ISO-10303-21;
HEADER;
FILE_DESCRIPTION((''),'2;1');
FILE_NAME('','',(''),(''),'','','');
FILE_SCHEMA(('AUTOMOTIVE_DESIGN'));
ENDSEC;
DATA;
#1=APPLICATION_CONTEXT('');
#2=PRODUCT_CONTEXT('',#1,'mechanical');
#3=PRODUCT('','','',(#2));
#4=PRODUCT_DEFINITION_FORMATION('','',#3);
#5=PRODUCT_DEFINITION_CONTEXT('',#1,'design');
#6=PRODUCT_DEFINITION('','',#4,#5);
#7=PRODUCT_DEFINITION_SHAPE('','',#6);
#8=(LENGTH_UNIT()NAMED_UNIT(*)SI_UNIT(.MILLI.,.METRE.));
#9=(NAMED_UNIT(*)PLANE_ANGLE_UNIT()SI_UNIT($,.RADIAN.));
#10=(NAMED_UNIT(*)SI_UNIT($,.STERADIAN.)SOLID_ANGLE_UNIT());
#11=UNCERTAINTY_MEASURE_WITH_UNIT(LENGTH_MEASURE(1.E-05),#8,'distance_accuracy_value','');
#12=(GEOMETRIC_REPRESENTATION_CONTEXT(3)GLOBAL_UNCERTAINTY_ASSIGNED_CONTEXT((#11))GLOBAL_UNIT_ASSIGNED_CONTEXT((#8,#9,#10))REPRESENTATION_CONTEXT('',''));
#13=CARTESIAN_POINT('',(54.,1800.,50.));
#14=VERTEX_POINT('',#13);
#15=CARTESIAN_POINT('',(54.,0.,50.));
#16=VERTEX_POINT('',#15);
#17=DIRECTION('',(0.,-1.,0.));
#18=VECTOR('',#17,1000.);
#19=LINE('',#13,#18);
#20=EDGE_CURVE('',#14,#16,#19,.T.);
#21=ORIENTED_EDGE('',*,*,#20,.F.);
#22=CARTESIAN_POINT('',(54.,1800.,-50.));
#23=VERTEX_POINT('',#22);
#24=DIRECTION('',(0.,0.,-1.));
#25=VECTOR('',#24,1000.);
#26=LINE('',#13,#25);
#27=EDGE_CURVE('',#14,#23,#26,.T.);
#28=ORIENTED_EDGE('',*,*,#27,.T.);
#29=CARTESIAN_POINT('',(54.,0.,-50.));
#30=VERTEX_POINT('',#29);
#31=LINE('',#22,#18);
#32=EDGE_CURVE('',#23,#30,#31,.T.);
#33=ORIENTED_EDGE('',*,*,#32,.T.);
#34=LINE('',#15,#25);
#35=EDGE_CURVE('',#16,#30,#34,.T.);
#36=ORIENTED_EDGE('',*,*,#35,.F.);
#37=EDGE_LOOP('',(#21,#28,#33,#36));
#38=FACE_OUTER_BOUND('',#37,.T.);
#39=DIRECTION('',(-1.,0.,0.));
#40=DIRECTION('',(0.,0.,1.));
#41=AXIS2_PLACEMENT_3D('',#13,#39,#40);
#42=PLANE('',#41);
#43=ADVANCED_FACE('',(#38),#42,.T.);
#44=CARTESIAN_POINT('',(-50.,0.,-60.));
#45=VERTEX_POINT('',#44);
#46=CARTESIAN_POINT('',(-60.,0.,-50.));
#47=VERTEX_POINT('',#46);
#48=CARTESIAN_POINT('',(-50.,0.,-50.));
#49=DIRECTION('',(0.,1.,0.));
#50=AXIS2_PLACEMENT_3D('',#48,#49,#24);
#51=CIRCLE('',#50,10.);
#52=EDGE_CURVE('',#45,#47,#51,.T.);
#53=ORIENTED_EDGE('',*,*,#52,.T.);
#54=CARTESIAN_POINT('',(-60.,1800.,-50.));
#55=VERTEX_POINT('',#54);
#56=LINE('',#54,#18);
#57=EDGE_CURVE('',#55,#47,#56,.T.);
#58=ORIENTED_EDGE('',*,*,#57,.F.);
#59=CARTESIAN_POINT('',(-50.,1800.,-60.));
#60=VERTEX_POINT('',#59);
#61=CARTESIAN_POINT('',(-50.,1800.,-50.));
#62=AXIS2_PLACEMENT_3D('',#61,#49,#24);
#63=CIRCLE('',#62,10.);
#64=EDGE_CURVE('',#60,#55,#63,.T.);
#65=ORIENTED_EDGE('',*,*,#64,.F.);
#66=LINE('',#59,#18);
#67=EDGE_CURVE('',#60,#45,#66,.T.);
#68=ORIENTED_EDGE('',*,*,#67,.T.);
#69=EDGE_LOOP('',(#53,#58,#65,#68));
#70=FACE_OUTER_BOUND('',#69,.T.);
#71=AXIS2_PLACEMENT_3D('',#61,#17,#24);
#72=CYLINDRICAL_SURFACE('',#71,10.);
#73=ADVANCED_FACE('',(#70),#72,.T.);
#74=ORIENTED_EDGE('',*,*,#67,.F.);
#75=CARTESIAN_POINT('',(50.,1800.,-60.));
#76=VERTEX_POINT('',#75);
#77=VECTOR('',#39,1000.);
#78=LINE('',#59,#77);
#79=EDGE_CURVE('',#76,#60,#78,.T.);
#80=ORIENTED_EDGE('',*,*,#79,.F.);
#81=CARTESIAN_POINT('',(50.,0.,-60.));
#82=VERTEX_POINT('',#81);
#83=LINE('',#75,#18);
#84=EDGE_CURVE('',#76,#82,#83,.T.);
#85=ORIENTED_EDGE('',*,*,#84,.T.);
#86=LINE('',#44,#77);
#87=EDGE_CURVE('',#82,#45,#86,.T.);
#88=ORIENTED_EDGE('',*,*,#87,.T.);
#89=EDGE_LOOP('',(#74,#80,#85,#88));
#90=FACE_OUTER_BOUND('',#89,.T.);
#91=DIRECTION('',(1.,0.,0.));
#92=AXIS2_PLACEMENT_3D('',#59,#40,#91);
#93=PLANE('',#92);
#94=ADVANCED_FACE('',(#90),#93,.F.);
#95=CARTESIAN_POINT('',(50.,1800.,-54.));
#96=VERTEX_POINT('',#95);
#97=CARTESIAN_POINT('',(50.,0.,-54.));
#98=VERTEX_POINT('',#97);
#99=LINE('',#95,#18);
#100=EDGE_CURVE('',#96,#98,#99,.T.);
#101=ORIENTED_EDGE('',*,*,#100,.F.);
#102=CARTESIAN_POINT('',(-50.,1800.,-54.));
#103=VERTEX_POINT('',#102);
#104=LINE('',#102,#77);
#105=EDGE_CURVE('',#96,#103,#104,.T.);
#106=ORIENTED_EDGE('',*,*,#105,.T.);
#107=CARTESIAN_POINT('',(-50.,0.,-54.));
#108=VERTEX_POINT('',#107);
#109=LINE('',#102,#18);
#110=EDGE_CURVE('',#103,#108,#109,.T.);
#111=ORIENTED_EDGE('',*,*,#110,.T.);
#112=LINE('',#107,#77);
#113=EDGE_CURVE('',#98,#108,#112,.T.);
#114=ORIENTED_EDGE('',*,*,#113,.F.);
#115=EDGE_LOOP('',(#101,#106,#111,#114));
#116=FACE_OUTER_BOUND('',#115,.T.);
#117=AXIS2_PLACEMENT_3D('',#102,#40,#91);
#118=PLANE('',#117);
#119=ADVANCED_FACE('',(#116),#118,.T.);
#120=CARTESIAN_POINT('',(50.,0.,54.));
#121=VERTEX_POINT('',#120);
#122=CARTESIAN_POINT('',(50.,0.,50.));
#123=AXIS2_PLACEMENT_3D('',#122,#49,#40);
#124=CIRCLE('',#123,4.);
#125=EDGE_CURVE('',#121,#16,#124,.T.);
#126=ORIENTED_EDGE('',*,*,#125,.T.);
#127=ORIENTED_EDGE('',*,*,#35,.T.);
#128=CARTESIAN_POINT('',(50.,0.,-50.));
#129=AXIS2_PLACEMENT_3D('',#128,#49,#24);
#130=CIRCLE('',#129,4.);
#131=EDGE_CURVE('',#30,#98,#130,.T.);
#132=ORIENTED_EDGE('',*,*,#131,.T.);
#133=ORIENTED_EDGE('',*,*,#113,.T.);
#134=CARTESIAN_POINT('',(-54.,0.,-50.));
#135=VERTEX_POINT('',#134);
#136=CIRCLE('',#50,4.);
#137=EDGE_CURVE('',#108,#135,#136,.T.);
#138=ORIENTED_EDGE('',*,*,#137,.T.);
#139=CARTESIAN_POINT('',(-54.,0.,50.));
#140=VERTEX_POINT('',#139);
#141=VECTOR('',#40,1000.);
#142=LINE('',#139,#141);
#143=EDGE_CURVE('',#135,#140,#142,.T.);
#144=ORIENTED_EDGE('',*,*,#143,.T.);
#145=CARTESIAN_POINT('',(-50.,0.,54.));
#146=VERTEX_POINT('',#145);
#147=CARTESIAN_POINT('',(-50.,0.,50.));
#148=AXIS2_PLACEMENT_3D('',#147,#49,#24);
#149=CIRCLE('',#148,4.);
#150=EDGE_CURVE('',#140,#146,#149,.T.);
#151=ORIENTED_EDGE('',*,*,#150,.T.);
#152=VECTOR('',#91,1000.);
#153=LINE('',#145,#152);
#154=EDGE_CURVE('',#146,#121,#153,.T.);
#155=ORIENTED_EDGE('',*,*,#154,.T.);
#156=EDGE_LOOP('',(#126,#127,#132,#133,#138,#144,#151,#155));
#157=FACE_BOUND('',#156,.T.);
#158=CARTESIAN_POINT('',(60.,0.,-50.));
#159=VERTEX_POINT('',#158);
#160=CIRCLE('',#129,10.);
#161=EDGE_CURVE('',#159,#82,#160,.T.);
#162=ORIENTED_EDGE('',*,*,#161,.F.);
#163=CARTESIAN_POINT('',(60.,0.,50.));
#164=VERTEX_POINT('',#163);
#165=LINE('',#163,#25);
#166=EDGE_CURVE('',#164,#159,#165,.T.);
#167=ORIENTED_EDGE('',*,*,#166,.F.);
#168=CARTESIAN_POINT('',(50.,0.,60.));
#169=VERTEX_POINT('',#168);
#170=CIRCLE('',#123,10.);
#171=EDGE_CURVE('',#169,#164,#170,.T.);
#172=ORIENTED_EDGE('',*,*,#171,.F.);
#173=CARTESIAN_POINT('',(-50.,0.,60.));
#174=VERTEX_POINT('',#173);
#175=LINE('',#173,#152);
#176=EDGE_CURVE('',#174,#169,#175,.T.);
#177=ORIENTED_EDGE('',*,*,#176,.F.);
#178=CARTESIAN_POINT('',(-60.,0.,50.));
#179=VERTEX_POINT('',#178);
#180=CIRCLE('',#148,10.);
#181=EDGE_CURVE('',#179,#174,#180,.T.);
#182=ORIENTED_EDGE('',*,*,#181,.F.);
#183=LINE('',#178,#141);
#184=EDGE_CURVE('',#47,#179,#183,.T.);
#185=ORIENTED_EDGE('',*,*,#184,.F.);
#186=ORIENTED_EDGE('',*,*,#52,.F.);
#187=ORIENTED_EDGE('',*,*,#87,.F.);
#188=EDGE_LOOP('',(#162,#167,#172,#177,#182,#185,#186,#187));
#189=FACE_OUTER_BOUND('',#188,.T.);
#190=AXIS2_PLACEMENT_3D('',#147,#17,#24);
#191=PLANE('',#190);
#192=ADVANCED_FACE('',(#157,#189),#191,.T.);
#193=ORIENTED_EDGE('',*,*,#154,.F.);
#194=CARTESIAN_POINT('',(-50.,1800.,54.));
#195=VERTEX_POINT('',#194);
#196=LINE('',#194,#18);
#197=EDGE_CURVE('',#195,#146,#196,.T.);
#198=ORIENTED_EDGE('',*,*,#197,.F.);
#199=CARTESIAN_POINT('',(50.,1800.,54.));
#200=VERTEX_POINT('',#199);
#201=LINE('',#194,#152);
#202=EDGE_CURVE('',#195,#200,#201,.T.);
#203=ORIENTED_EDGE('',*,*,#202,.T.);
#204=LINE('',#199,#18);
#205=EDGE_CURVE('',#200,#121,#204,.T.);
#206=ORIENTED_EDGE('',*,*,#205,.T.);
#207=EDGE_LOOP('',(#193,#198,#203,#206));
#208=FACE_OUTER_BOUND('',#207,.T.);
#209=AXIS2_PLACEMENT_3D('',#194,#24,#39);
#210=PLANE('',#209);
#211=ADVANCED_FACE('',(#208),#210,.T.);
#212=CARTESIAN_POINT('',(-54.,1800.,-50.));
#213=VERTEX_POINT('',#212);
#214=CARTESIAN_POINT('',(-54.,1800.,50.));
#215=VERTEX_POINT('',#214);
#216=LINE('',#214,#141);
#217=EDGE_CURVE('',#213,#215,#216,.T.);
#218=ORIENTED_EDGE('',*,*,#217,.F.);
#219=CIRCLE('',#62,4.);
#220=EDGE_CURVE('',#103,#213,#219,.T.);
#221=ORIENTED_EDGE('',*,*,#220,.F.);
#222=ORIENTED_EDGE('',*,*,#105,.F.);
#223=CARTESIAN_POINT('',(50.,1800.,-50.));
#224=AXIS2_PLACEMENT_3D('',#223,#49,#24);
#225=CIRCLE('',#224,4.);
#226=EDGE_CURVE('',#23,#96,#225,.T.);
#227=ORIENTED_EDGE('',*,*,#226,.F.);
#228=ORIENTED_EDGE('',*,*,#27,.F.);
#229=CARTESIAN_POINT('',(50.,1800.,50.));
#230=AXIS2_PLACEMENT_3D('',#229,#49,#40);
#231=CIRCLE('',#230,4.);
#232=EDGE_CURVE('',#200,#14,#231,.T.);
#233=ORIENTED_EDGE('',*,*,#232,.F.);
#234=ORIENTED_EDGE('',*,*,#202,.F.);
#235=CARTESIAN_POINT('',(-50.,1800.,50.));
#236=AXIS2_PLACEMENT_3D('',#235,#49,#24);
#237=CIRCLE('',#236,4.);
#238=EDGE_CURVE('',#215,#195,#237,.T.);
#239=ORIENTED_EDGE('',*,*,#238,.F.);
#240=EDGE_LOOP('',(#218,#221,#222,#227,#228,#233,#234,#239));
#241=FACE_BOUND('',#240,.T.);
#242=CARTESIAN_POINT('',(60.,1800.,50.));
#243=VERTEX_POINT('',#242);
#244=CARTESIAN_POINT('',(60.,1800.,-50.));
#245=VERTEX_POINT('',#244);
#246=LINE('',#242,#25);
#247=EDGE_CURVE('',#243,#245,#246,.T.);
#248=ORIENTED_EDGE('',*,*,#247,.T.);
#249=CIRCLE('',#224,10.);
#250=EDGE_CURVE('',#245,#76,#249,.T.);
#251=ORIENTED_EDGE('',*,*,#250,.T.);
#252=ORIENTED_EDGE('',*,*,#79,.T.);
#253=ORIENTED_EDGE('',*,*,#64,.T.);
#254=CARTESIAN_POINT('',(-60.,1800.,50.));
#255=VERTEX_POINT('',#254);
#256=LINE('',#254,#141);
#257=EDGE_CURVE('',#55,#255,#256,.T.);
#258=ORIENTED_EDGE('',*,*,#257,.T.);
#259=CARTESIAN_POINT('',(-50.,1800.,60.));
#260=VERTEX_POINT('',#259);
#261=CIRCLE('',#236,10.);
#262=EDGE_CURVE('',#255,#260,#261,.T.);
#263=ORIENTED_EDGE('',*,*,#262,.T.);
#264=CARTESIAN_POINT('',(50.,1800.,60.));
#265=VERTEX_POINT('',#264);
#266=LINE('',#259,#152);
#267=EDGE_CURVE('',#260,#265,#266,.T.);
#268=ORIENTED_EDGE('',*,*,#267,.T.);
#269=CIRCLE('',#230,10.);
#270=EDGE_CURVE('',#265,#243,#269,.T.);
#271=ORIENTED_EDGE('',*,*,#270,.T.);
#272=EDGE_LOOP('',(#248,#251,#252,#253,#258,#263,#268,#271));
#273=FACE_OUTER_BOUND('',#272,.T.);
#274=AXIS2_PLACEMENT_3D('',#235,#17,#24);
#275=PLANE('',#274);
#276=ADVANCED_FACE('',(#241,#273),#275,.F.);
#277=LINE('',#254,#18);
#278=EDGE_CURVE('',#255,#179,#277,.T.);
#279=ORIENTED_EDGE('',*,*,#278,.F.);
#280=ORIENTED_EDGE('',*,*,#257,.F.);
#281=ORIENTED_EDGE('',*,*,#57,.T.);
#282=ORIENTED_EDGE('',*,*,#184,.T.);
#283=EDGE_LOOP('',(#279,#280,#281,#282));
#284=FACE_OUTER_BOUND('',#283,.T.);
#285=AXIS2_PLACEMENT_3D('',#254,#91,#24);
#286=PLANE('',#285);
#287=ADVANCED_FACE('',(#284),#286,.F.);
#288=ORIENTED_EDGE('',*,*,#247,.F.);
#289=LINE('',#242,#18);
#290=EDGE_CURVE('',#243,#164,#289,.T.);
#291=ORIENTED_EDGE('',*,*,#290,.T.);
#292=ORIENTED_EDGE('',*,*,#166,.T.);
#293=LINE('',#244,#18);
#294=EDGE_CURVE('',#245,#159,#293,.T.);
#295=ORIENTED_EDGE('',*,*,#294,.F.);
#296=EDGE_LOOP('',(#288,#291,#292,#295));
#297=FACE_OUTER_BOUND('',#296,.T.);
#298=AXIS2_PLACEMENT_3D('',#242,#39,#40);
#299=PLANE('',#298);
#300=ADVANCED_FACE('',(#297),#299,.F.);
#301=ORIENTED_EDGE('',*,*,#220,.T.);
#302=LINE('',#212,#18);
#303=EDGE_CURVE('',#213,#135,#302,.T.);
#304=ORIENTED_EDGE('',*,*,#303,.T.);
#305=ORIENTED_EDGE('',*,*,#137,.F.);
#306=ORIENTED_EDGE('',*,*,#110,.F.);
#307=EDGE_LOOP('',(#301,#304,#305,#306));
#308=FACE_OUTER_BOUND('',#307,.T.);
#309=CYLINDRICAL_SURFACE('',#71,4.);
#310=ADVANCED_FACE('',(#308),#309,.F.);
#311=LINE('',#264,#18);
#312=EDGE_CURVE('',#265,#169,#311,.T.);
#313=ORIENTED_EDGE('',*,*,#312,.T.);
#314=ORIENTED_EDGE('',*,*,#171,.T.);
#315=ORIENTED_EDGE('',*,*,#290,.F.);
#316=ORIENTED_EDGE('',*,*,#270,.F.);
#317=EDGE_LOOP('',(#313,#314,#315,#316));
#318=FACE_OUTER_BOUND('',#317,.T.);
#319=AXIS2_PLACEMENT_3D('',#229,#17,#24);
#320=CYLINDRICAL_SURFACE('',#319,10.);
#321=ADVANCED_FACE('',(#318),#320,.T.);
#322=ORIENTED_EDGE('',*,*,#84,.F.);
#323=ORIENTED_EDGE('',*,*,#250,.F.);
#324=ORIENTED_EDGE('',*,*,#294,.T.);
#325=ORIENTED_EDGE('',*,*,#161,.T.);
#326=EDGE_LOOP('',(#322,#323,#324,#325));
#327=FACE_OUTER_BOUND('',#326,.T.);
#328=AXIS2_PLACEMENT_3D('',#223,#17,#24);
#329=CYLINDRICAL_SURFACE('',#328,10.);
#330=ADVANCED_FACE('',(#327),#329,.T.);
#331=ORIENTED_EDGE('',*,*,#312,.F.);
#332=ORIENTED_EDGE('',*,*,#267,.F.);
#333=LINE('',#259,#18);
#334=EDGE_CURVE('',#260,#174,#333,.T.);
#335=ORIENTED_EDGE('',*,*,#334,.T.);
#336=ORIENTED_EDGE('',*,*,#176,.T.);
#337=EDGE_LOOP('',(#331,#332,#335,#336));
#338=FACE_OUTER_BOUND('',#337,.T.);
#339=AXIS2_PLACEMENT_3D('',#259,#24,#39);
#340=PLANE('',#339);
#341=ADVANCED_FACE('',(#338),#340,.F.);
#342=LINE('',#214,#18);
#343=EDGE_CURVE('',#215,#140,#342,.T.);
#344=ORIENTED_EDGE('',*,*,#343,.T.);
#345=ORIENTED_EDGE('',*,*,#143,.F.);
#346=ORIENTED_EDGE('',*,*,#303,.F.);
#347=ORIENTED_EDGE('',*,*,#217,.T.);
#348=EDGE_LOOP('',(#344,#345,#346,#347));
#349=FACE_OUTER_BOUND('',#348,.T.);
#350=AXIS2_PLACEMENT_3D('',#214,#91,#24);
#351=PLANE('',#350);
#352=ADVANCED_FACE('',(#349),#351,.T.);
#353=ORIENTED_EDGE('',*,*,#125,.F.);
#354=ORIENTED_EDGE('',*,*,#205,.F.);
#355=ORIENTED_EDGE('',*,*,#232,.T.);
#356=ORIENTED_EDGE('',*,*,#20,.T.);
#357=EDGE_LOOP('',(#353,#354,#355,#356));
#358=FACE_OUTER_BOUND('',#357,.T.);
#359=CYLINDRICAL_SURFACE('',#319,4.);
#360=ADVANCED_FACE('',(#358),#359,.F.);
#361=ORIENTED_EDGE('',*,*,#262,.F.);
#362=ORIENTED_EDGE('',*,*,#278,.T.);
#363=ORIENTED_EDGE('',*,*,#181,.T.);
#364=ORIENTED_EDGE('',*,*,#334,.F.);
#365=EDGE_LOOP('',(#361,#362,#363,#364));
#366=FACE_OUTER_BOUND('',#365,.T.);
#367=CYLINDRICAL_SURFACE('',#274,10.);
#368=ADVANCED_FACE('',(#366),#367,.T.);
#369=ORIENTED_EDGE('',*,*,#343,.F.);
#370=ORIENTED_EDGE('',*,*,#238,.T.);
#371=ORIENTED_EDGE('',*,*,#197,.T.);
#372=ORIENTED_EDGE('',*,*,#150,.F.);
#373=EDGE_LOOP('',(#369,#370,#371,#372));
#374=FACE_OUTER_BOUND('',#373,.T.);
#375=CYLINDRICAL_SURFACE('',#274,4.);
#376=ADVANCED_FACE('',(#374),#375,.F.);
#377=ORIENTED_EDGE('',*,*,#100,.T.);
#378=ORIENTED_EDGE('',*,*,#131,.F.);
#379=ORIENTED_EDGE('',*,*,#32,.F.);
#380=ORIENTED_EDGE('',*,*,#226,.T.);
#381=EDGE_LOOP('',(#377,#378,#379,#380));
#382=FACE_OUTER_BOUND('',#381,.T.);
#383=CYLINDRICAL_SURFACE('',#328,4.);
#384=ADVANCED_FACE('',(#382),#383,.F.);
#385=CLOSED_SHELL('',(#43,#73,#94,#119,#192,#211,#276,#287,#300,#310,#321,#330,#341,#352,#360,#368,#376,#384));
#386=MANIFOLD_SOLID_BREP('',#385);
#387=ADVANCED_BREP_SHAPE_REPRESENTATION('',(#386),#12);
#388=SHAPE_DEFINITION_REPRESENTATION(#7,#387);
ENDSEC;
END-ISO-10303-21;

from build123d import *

# Parameters (mm, degrees)
BOSS_EXTRUDE1_DEPTH = 1800


with BuildPart() as part:
    # Sketch1 → Boss-Extrude1 (new body)
    with BuildSketch(Plane(origin=(0, 0, 0), x_dir=(1, 0, 0), z_dir=(0, 1, 0))):
        with BuildLine():
            Line((-50, -60), (50, -60))
            ThreePointArc((50, -60), (57.071067812, -57.071067812), (60, -50))
            Line((60, -50), (60, 50))
            ThreePointArc((60, 50), (57.071067812, 57.071067812), (50, 60))
            Line((50, 60), (-50, 60))
            ThreePointArc((-50, 60), (-57.071067812, 57.071067812), (-60, 50))
            Line((-60, 50), (-60, -50))
            ThreePointArc((-60, -50), (-57.071067812, -57.071067812), (-50, -60))
        make_face()
        with BuildLine():
            Line((-54, -50), (-54, 50))
            ThreePointArc((-54, 50), (-52.828427125, 52.828427125), (-50, 54))
            Line((-50, 54), (50, 54))
            ThreePointArc((50, 54), (52.828427125, 52.828427125), (54, 50))
            Line((54, 50), (54, -50))
            ThreePointArc((54, -50), (52.828427125, -52.828427125), (50, -54))
            Line((50, -54), (-50, -54))
            ThreePointArc((-50, -54), (-52.828427125, -52.828427125), (-54, -50))
        make_face(mode=Mode.SUBTRACT)
    extrude(amount=BOSS_EXTRUDE1_DEPTH)


solid = part.part
